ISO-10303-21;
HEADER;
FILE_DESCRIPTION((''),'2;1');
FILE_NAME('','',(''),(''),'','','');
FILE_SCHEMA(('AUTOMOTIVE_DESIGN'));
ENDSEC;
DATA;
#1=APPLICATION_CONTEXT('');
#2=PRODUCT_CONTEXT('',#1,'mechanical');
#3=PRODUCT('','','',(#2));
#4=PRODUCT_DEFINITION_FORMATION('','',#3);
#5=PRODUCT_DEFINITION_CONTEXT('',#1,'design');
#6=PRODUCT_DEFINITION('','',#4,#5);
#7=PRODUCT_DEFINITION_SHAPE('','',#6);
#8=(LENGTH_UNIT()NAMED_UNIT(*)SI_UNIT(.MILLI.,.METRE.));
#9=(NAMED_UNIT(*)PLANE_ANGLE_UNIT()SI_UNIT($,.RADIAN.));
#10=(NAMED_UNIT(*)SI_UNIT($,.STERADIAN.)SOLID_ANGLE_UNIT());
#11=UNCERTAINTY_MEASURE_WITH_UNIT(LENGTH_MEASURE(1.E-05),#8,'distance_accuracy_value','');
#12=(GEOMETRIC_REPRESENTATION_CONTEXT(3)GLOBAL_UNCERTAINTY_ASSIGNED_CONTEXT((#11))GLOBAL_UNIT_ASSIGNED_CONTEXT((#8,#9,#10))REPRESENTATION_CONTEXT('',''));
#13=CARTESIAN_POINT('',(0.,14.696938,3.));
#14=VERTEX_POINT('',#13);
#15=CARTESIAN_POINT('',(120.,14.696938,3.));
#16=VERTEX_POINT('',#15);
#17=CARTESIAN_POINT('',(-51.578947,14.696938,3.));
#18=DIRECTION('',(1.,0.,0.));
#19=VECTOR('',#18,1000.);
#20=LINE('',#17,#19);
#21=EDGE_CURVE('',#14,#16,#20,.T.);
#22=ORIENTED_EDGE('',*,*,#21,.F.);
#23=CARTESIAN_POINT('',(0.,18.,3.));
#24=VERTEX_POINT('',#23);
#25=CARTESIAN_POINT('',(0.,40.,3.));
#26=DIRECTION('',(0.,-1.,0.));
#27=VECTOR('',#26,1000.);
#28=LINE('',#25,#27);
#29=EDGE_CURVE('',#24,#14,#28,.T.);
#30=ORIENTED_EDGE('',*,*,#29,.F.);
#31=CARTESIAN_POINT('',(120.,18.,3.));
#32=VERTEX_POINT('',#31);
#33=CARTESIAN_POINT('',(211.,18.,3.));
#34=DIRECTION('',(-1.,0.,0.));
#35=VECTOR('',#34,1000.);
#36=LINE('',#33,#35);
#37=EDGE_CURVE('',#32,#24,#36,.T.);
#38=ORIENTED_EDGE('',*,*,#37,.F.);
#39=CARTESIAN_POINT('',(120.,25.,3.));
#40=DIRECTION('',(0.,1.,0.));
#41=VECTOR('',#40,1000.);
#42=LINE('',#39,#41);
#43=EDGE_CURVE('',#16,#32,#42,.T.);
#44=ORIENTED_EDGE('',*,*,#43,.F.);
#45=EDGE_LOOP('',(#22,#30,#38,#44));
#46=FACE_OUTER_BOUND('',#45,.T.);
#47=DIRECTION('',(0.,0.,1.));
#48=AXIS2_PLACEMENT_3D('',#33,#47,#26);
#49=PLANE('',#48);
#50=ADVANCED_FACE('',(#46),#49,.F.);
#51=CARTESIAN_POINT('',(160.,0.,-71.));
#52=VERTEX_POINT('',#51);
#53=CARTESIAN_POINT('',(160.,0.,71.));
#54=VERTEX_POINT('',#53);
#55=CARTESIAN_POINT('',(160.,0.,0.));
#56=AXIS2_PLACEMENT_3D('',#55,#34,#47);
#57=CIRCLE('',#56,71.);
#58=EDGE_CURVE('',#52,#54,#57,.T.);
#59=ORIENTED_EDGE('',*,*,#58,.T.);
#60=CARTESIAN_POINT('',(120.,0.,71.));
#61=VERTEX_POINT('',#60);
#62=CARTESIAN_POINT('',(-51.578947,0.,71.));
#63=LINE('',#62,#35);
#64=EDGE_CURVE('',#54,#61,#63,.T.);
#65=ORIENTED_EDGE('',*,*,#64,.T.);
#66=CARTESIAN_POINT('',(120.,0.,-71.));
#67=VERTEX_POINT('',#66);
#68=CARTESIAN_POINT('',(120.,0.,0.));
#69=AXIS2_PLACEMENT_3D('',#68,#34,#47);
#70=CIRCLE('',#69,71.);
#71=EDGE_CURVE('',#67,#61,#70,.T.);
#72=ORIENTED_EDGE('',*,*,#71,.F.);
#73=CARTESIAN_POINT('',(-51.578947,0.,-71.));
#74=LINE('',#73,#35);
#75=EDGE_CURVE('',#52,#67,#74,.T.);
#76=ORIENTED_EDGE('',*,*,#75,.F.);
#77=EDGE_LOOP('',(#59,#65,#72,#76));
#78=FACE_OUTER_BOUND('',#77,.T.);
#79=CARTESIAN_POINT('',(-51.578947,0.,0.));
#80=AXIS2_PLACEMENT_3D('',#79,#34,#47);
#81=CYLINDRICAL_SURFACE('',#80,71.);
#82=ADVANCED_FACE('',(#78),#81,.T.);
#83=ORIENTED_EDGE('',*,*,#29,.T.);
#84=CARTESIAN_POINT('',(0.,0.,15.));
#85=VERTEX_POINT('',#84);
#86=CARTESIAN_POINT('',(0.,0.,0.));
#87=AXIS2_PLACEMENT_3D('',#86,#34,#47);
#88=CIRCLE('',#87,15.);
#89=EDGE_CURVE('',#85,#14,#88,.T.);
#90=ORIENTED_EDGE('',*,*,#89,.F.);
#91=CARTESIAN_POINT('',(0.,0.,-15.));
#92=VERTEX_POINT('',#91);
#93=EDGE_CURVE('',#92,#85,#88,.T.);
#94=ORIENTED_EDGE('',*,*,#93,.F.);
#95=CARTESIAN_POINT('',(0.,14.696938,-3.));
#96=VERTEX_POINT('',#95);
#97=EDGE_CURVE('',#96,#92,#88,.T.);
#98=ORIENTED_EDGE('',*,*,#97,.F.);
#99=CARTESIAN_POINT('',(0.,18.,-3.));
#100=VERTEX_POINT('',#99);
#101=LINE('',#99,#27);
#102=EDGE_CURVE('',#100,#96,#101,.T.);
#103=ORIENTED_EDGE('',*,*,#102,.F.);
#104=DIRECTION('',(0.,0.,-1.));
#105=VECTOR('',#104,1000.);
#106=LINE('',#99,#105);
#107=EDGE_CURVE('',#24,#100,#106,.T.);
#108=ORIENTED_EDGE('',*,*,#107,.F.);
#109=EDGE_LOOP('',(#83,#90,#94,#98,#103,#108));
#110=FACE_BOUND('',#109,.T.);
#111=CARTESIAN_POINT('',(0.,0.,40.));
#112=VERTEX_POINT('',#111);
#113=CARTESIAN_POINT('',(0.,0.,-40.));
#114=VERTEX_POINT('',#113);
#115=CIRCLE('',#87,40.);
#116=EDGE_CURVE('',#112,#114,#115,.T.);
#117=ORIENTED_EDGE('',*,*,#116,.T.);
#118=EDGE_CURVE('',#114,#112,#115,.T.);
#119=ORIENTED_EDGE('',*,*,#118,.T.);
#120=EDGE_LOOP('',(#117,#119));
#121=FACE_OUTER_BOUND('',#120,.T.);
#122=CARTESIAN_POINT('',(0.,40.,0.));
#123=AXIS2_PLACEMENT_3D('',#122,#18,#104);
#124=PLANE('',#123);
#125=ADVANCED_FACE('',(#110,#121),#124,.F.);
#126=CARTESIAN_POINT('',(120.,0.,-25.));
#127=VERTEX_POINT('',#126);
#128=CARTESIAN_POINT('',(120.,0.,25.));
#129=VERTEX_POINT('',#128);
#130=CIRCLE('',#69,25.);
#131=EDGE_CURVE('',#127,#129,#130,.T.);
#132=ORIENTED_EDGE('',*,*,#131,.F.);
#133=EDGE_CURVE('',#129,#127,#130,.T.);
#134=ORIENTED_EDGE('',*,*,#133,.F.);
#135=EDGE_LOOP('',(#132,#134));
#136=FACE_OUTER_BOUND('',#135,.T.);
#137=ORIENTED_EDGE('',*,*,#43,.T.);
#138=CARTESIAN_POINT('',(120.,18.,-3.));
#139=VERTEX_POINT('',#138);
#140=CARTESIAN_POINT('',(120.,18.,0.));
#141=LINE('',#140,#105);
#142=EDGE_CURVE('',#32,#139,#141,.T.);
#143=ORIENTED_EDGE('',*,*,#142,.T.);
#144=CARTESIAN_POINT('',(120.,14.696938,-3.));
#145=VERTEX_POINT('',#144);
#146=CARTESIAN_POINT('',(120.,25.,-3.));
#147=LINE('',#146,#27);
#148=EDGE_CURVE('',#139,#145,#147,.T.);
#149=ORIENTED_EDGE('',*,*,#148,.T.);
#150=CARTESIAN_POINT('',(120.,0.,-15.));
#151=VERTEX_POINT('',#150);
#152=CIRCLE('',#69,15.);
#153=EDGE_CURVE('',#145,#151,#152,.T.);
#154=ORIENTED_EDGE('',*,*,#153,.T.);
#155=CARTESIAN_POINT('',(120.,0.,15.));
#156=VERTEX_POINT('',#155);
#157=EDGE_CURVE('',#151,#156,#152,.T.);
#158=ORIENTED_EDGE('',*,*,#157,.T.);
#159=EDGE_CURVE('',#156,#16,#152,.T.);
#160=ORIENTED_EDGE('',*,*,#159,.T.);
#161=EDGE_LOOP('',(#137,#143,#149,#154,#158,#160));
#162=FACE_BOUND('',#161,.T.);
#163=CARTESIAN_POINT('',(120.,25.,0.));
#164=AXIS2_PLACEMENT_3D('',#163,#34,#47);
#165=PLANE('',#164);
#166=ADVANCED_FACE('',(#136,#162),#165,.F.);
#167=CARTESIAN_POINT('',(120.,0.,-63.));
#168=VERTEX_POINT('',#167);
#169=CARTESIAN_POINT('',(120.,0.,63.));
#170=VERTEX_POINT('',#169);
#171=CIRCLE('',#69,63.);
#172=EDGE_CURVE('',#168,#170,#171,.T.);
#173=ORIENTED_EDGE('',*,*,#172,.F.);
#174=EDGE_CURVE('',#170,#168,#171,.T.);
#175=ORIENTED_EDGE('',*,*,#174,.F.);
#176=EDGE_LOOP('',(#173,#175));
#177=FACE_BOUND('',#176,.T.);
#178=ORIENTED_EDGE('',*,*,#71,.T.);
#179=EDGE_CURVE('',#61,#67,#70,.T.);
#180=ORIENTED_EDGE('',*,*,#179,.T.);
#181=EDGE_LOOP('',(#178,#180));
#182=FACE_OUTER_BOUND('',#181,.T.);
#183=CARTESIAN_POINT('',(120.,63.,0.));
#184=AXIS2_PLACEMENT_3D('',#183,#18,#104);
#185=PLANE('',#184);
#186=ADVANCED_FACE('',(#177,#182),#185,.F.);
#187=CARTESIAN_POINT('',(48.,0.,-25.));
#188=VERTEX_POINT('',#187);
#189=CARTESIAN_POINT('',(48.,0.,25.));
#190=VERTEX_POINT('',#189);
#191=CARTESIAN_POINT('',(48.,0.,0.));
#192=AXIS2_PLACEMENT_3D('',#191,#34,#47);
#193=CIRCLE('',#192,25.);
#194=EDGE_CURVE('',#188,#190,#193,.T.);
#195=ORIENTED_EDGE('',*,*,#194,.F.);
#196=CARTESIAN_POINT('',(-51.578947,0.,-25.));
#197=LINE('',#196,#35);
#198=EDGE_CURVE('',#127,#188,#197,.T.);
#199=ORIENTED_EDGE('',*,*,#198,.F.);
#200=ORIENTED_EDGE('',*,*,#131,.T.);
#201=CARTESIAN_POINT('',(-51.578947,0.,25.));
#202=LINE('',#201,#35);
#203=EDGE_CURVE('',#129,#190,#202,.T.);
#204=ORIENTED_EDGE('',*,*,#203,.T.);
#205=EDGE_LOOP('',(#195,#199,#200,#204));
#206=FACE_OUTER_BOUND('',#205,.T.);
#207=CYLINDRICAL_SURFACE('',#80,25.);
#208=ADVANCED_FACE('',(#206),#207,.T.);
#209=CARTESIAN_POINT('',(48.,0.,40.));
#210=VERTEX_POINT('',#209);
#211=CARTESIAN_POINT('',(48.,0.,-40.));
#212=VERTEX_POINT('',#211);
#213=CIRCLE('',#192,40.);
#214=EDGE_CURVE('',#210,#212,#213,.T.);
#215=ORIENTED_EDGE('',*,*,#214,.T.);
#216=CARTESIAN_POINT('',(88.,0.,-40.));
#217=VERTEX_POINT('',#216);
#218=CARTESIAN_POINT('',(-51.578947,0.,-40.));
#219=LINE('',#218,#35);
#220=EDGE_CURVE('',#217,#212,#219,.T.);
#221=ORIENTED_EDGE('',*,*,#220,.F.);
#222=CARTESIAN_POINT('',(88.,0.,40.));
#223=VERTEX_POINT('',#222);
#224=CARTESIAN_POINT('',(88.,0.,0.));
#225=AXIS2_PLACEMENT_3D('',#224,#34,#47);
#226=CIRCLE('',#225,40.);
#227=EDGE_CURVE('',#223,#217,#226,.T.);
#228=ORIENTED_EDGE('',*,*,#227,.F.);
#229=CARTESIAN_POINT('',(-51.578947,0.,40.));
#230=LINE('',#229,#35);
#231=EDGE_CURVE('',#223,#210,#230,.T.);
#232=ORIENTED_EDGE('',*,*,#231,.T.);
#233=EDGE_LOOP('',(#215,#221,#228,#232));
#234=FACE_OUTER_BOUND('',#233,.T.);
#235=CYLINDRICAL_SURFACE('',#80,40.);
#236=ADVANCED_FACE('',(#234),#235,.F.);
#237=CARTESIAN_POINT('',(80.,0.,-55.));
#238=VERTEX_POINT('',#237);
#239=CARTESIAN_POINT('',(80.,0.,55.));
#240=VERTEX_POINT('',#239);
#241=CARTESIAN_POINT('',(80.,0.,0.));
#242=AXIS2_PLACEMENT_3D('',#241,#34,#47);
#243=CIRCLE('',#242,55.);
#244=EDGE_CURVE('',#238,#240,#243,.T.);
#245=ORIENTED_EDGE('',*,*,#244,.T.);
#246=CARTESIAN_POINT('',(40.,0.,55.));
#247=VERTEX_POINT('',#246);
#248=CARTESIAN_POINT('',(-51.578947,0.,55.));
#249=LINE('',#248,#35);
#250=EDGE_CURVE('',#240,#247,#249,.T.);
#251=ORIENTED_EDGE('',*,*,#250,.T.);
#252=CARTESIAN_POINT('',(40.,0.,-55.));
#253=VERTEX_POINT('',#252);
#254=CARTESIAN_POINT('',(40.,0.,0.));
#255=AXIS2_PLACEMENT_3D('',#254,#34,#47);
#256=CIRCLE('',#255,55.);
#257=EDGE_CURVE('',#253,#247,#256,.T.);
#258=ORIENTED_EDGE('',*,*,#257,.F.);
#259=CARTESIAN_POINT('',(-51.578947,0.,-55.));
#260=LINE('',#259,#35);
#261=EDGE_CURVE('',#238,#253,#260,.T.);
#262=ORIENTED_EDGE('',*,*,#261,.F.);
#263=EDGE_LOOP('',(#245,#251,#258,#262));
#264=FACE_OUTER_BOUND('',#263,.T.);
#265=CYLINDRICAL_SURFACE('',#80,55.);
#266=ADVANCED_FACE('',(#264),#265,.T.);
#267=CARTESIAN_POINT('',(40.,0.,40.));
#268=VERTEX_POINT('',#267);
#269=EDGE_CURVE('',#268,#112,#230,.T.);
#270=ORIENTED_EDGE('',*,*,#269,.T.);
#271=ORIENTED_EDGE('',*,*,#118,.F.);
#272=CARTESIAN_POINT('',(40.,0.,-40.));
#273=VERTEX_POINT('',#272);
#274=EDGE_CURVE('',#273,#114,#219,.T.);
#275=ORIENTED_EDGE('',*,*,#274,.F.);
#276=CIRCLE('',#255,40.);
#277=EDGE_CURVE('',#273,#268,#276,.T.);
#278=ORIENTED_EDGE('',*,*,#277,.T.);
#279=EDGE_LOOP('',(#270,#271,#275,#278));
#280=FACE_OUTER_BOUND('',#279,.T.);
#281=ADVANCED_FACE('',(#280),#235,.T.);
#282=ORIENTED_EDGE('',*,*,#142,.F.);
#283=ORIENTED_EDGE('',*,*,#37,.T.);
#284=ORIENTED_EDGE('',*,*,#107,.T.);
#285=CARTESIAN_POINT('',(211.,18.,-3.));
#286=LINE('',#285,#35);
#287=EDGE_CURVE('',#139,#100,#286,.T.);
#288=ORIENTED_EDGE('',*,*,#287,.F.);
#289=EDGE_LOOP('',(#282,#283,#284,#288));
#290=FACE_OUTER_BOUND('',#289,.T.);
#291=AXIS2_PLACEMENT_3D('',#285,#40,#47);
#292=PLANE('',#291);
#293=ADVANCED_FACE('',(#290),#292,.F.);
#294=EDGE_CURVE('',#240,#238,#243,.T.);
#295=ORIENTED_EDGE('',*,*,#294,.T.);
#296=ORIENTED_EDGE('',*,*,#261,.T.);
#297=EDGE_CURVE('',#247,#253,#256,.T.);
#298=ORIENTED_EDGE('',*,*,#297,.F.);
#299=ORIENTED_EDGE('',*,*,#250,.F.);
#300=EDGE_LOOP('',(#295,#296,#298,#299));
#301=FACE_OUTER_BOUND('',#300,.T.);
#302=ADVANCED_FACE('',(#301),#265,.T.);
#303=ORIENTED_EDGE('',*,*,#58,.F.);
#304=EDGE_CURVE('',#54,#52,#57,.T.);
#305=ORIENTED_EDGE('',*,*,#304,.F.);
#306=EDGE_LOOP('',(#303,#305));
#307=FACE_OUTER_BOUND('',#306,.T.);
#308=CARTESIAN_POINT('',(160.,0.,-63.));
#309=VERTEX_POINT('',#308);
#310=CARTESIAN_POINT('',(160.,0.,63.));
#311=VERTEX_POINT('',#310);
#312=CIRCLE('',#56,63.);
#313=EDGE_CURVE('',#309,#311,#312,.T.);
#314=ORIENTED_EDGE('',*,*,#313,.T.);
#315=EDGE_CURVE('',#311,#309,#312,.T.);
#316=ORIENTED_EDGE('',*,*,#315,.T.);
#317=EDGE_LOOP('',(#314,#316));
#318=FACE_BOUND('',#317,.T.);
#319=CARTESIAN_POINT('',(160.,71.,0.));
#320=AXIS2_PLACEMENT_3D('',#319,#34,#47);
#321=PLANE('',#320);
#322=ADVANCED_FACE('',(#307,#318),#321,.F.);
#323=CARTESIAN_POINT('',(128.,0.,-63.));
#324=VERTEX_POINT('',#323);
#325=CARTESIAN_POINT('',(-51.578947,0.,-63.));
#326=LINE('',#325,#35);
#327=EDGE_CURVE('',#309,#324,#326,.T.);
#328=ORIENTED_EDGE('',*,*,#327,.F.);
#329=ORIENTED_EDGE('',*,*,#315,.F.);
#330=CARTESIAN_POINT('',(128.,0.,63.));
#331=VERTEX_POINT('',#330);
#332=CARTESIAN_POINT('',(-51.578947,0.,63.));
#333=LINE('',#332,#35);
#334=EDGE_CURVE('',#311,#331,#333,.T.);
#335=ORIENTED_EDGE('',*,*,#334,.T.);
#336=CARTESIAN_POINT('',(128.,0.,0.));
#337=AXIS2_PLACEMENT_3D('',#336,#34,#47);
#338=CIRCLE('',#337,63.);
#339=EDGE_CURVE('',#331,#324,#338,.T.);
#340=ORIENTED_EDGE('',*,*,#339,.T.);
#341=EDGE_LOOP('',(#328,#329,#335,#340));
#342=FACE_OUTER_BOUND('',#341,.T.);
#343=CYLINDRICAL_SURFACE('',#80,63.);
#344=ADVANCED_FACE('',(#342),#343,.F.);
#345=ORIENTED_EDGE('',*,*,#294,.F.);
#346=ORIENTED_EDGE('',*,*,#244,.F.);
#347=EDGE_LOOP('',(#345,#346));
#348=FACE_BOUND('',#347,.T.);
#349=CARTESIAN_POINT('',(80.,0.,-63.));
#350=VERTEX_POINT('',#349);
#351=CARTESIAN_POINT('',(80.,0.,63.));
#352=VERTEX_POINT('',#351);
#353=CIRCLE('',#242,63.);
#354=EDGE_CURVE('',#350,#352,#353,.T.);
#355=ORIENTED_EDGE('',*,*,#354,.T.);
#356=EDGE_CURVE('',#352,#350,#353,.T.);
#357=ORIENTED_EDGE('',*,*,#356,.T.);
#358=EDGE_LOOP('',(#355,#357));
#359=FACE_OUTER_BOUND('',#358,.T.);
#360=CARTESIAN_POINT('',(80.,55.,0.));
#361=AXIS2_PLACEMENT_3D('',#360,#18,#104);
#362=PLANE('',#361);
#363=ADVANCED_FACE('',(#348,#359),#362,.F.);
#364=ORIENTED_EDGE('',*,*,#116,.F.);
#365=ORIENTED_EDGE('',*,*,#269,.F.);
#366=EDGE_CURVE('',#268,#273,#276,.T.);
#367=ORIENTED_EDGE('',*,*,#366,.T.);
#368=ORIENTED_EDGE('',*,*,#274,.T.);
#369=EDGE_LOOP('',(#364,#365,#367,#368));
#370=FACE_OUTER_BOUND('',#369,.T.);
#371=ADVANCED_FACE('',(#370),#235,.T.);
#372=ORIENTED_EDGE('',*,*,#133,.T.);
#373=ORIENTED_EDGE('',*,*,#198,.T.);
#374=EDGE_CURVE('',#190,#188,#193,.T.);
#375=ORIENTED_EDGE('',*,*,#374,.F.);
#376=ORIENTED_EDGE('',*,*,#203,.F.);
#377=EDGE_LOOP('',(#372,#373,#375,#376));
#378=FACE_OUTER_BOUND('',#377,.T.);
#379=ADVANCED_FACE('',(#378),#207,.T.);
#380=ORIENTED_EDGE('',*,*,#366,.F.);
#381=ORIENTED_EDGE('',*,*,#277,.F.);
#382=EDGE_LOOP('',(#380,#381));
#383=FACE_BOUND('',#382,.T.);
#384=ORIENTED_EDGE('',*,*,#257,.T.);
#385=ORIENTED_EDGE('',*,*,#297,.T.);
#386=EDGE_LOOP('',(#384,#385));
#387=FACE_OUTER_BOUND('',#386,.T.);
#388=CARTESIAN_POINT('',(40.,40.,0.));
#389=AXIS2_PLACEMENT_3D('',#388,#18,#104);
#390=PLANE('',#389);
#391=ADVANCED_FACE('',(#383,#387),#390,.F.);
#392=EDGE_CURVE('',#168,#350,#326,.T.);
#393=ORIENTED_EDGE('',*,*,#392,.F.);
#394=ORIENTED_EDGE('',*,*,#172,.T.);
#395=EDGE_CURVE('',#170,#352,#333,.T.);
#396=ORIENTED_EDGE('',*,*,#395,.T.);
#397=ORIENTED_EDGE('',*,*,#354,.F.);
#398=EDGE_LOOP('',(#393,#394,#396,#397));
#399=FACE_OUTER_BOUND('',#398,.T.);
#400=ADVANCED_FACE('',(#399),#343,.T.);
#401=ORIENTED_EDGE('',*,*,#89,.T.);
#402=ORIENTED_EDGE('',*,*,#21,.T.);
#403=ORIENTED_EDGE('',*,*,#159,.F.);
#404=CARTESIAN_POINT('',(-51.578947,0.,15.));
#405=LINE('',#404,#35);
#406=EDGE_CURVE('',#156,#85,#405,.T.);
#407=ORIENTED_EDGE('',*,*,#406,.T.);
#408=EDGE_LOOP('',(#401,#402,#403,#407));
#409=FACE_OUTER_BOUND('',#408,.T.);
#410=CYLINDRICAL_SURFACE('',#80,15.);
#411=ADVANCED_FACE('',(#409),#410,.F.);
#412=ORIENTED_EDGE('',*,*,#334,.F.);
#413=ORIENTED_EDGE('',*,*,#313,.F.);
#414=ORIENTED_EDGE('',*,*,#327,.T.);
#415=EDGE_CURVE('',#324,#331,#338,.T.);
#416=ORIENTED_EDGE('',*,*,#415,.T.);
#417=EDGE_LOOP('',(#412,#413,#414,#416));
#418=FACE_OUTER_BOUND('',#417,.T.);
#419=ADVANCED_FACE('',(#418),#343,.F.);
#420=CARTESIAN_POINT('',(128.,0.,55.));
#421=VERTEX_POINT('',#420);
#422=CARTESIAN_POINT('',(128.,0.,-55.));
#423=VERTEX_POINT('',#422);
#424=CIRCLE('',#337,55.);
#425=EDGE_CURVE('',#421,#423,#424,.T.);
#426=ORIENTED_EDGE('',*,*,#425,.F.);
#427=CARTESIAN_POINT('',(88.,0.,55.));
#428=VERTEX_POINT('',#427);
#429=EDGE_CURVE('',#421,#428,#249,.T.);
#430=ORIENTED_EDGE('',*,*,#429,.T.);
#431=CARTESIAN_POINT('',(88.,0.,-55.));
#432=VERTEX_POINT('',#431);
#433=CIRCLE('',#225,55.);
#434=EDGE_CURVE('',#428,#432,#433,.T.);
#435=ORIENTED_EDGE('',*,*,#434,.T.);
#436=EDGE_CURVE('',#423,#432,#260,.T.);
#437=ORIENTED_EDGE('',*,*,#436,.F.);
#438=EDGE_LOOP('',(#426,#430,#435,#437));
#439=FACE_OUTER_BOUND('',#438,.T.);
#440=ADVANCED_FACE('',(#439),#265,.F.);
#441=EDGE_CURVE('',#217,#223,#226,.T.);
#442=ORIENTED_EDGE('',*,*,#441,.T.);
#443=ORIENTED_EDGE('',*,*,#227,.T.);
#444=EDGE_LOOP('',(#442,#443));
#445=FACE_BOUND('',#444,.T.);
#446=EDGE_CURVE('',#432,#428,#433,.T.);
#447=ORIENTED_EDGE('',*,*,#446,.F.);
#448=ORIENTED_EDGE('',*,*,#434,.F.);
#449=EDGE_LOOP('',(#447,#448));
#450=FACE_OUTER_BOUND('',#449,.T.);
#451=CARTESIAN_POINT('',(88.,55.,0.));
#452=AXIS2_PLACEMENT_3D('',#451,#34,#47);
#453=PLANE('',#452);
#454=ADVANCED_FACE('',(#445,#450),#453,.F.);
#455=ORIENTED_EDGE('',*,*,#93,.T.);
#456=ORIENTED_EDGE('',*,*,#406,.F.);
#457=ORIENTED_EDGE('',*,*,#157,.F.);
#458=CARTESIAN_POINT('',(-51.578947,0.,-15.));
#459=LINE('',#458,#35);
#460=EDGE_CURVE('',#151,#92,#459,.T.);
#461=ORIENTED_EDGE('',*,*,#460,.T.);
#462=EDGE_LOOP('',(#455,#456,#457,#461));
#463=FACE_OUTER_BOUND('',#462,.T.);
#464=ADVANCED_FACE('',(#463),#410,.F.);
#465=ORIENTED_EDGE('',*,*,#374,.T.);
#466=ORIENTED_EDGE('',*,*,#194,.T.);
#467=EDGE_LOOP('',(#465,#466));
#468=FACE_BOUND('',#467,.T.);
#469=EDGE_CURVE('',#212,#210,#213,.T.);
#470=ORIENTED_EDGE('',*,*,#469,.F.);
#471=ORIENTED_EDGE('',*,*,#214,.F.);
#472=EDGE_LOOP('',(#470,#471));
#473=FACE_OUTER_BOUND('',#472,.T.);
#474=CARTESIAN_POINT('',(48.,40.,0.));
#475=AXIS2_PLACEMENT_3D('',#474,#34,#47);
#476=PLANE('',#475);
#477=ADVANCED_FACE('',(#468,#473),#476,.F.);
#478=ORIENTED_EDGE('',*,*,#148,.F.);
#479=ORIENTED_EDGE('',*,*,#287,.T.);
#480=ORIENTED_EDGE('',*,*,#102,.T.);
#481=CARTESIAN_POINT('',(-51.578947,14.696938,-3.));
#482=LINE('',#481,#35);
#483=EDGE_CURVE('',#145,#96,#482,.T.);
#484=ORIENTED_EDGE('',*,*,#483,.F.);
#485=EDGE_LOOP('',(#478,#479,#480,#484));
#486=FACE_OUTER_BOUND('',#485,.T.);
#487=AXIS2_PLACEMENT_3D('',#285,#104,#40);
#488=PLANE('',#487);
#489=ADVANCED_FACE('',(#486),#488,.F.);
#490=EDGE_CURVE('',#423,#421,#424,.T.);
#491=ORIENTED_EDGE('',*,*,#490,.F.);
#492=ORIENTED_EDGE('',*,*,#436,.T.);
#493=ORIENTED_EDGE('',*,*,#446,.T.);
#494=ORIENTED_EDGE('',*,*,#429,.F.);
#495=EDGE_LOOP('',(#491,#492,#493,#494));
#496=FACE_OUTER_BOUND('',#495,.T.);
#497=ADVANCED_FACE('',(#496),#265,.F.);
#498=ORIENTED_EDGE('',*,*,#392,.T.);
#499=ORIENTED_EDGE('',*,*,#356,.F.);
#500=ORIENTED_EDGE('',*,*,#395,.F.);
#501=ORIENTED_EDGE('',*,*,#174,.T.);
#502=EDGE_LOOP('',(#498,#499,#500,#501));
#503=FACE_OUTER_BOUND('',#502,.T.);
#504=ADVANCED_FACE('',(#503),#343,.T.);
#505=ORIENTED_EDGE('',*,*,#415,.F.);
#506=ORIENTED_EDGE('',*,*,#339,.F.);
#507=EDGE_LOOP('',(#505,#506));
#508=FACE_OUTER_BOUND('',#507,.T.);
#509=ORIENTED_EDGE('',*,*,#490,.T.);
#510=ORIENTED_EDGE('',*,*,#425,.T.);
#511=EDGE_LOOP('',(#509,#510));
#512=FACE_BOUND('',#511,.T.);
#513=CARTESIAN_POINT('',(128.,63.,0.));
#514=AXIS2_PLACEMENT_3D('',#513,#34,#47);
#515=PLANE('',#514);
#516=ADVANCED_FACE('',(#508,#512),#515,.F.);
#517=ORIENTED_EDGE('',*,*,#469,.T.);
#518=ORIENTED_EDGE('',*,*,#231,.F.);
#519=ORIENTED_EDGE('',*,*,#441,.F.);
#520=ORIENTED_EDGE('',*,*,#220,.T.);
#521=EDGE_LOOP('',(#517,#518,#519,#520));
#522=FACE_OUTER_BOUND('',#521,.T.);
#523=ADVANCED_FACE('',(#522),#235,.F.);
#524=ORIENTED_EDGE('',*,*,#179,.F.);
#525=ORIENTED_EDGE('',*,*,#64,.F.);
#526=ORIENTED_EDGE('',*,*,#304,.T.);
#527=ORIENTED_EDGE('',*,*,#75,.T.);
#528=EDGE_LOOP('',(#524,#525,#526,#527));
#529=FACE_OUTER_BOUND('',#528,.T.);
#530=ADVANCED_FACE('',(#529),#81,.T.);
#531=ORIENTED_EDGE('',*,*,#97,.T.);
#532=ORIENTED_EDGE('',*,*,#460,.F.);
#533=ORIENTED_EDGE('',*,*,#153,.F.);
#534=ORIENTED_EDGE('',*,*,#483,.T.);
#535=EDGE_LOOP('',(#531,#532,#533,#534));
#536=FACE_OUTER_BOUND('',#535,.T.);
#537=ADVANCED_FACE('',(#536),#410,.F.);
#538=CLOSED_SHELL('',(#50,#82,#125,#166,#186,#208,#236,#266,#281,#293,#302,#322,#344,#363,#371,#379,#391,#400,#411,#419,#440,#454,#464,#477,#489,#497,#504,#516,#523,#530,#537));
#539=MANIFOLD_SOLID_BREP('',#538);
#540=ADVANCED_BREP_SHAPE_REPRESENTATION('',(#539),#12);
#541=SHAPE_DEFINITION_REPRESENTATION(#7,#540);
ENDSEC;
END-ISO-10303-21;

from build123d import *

# Parameters (mm, degrees)
KEYWAY_PROFILE_6X6_W = 6
KEYWAY_PROFILE_6X6_H = 6
KEYWAY_CUT_6X6_DEPTH = 211


with BuildPart() as part:
    # Pulley Step Profile → Stepped Pulley Body (revolve)
    with BuildSketch(Plane.XY, mode=Mode.PRIVATE) as stepped_pulley_body_sk:
        Polygon((0, 40), (0, 15), (120, 15), (120, 25), (48, 25), (48, 40), (88, 40), (88, 55), (128, 55), (128, 63), (160, 63), (160, 71), (120, 71), (120, 63), (80, 63), (80, 55), (40, 55), (40, 40), align=None)
    revolve(stepped_pulley_body_sk.sketch.rotate(Axis((-51.578947368, 0, 0), (1, 0, 0)), 90), axis=Axis((-51.578947368, 0, 0), (1, 0, 0)))

    # Keyway Profile 6x6 → Keyway Cut 6x6 (cut)
    with BuildSketch(Plane.ZY):
        with Locations((0, 15)):
            Rectangle(KEYWAY_PROFILE_6X6_W, KEYWAY_PROFILE_6X6_H)
    extrude(amount=-KEYWAY_CUT_6X6_DEPTH, mode=Mode.SUBTRACT)


solid = part.part
